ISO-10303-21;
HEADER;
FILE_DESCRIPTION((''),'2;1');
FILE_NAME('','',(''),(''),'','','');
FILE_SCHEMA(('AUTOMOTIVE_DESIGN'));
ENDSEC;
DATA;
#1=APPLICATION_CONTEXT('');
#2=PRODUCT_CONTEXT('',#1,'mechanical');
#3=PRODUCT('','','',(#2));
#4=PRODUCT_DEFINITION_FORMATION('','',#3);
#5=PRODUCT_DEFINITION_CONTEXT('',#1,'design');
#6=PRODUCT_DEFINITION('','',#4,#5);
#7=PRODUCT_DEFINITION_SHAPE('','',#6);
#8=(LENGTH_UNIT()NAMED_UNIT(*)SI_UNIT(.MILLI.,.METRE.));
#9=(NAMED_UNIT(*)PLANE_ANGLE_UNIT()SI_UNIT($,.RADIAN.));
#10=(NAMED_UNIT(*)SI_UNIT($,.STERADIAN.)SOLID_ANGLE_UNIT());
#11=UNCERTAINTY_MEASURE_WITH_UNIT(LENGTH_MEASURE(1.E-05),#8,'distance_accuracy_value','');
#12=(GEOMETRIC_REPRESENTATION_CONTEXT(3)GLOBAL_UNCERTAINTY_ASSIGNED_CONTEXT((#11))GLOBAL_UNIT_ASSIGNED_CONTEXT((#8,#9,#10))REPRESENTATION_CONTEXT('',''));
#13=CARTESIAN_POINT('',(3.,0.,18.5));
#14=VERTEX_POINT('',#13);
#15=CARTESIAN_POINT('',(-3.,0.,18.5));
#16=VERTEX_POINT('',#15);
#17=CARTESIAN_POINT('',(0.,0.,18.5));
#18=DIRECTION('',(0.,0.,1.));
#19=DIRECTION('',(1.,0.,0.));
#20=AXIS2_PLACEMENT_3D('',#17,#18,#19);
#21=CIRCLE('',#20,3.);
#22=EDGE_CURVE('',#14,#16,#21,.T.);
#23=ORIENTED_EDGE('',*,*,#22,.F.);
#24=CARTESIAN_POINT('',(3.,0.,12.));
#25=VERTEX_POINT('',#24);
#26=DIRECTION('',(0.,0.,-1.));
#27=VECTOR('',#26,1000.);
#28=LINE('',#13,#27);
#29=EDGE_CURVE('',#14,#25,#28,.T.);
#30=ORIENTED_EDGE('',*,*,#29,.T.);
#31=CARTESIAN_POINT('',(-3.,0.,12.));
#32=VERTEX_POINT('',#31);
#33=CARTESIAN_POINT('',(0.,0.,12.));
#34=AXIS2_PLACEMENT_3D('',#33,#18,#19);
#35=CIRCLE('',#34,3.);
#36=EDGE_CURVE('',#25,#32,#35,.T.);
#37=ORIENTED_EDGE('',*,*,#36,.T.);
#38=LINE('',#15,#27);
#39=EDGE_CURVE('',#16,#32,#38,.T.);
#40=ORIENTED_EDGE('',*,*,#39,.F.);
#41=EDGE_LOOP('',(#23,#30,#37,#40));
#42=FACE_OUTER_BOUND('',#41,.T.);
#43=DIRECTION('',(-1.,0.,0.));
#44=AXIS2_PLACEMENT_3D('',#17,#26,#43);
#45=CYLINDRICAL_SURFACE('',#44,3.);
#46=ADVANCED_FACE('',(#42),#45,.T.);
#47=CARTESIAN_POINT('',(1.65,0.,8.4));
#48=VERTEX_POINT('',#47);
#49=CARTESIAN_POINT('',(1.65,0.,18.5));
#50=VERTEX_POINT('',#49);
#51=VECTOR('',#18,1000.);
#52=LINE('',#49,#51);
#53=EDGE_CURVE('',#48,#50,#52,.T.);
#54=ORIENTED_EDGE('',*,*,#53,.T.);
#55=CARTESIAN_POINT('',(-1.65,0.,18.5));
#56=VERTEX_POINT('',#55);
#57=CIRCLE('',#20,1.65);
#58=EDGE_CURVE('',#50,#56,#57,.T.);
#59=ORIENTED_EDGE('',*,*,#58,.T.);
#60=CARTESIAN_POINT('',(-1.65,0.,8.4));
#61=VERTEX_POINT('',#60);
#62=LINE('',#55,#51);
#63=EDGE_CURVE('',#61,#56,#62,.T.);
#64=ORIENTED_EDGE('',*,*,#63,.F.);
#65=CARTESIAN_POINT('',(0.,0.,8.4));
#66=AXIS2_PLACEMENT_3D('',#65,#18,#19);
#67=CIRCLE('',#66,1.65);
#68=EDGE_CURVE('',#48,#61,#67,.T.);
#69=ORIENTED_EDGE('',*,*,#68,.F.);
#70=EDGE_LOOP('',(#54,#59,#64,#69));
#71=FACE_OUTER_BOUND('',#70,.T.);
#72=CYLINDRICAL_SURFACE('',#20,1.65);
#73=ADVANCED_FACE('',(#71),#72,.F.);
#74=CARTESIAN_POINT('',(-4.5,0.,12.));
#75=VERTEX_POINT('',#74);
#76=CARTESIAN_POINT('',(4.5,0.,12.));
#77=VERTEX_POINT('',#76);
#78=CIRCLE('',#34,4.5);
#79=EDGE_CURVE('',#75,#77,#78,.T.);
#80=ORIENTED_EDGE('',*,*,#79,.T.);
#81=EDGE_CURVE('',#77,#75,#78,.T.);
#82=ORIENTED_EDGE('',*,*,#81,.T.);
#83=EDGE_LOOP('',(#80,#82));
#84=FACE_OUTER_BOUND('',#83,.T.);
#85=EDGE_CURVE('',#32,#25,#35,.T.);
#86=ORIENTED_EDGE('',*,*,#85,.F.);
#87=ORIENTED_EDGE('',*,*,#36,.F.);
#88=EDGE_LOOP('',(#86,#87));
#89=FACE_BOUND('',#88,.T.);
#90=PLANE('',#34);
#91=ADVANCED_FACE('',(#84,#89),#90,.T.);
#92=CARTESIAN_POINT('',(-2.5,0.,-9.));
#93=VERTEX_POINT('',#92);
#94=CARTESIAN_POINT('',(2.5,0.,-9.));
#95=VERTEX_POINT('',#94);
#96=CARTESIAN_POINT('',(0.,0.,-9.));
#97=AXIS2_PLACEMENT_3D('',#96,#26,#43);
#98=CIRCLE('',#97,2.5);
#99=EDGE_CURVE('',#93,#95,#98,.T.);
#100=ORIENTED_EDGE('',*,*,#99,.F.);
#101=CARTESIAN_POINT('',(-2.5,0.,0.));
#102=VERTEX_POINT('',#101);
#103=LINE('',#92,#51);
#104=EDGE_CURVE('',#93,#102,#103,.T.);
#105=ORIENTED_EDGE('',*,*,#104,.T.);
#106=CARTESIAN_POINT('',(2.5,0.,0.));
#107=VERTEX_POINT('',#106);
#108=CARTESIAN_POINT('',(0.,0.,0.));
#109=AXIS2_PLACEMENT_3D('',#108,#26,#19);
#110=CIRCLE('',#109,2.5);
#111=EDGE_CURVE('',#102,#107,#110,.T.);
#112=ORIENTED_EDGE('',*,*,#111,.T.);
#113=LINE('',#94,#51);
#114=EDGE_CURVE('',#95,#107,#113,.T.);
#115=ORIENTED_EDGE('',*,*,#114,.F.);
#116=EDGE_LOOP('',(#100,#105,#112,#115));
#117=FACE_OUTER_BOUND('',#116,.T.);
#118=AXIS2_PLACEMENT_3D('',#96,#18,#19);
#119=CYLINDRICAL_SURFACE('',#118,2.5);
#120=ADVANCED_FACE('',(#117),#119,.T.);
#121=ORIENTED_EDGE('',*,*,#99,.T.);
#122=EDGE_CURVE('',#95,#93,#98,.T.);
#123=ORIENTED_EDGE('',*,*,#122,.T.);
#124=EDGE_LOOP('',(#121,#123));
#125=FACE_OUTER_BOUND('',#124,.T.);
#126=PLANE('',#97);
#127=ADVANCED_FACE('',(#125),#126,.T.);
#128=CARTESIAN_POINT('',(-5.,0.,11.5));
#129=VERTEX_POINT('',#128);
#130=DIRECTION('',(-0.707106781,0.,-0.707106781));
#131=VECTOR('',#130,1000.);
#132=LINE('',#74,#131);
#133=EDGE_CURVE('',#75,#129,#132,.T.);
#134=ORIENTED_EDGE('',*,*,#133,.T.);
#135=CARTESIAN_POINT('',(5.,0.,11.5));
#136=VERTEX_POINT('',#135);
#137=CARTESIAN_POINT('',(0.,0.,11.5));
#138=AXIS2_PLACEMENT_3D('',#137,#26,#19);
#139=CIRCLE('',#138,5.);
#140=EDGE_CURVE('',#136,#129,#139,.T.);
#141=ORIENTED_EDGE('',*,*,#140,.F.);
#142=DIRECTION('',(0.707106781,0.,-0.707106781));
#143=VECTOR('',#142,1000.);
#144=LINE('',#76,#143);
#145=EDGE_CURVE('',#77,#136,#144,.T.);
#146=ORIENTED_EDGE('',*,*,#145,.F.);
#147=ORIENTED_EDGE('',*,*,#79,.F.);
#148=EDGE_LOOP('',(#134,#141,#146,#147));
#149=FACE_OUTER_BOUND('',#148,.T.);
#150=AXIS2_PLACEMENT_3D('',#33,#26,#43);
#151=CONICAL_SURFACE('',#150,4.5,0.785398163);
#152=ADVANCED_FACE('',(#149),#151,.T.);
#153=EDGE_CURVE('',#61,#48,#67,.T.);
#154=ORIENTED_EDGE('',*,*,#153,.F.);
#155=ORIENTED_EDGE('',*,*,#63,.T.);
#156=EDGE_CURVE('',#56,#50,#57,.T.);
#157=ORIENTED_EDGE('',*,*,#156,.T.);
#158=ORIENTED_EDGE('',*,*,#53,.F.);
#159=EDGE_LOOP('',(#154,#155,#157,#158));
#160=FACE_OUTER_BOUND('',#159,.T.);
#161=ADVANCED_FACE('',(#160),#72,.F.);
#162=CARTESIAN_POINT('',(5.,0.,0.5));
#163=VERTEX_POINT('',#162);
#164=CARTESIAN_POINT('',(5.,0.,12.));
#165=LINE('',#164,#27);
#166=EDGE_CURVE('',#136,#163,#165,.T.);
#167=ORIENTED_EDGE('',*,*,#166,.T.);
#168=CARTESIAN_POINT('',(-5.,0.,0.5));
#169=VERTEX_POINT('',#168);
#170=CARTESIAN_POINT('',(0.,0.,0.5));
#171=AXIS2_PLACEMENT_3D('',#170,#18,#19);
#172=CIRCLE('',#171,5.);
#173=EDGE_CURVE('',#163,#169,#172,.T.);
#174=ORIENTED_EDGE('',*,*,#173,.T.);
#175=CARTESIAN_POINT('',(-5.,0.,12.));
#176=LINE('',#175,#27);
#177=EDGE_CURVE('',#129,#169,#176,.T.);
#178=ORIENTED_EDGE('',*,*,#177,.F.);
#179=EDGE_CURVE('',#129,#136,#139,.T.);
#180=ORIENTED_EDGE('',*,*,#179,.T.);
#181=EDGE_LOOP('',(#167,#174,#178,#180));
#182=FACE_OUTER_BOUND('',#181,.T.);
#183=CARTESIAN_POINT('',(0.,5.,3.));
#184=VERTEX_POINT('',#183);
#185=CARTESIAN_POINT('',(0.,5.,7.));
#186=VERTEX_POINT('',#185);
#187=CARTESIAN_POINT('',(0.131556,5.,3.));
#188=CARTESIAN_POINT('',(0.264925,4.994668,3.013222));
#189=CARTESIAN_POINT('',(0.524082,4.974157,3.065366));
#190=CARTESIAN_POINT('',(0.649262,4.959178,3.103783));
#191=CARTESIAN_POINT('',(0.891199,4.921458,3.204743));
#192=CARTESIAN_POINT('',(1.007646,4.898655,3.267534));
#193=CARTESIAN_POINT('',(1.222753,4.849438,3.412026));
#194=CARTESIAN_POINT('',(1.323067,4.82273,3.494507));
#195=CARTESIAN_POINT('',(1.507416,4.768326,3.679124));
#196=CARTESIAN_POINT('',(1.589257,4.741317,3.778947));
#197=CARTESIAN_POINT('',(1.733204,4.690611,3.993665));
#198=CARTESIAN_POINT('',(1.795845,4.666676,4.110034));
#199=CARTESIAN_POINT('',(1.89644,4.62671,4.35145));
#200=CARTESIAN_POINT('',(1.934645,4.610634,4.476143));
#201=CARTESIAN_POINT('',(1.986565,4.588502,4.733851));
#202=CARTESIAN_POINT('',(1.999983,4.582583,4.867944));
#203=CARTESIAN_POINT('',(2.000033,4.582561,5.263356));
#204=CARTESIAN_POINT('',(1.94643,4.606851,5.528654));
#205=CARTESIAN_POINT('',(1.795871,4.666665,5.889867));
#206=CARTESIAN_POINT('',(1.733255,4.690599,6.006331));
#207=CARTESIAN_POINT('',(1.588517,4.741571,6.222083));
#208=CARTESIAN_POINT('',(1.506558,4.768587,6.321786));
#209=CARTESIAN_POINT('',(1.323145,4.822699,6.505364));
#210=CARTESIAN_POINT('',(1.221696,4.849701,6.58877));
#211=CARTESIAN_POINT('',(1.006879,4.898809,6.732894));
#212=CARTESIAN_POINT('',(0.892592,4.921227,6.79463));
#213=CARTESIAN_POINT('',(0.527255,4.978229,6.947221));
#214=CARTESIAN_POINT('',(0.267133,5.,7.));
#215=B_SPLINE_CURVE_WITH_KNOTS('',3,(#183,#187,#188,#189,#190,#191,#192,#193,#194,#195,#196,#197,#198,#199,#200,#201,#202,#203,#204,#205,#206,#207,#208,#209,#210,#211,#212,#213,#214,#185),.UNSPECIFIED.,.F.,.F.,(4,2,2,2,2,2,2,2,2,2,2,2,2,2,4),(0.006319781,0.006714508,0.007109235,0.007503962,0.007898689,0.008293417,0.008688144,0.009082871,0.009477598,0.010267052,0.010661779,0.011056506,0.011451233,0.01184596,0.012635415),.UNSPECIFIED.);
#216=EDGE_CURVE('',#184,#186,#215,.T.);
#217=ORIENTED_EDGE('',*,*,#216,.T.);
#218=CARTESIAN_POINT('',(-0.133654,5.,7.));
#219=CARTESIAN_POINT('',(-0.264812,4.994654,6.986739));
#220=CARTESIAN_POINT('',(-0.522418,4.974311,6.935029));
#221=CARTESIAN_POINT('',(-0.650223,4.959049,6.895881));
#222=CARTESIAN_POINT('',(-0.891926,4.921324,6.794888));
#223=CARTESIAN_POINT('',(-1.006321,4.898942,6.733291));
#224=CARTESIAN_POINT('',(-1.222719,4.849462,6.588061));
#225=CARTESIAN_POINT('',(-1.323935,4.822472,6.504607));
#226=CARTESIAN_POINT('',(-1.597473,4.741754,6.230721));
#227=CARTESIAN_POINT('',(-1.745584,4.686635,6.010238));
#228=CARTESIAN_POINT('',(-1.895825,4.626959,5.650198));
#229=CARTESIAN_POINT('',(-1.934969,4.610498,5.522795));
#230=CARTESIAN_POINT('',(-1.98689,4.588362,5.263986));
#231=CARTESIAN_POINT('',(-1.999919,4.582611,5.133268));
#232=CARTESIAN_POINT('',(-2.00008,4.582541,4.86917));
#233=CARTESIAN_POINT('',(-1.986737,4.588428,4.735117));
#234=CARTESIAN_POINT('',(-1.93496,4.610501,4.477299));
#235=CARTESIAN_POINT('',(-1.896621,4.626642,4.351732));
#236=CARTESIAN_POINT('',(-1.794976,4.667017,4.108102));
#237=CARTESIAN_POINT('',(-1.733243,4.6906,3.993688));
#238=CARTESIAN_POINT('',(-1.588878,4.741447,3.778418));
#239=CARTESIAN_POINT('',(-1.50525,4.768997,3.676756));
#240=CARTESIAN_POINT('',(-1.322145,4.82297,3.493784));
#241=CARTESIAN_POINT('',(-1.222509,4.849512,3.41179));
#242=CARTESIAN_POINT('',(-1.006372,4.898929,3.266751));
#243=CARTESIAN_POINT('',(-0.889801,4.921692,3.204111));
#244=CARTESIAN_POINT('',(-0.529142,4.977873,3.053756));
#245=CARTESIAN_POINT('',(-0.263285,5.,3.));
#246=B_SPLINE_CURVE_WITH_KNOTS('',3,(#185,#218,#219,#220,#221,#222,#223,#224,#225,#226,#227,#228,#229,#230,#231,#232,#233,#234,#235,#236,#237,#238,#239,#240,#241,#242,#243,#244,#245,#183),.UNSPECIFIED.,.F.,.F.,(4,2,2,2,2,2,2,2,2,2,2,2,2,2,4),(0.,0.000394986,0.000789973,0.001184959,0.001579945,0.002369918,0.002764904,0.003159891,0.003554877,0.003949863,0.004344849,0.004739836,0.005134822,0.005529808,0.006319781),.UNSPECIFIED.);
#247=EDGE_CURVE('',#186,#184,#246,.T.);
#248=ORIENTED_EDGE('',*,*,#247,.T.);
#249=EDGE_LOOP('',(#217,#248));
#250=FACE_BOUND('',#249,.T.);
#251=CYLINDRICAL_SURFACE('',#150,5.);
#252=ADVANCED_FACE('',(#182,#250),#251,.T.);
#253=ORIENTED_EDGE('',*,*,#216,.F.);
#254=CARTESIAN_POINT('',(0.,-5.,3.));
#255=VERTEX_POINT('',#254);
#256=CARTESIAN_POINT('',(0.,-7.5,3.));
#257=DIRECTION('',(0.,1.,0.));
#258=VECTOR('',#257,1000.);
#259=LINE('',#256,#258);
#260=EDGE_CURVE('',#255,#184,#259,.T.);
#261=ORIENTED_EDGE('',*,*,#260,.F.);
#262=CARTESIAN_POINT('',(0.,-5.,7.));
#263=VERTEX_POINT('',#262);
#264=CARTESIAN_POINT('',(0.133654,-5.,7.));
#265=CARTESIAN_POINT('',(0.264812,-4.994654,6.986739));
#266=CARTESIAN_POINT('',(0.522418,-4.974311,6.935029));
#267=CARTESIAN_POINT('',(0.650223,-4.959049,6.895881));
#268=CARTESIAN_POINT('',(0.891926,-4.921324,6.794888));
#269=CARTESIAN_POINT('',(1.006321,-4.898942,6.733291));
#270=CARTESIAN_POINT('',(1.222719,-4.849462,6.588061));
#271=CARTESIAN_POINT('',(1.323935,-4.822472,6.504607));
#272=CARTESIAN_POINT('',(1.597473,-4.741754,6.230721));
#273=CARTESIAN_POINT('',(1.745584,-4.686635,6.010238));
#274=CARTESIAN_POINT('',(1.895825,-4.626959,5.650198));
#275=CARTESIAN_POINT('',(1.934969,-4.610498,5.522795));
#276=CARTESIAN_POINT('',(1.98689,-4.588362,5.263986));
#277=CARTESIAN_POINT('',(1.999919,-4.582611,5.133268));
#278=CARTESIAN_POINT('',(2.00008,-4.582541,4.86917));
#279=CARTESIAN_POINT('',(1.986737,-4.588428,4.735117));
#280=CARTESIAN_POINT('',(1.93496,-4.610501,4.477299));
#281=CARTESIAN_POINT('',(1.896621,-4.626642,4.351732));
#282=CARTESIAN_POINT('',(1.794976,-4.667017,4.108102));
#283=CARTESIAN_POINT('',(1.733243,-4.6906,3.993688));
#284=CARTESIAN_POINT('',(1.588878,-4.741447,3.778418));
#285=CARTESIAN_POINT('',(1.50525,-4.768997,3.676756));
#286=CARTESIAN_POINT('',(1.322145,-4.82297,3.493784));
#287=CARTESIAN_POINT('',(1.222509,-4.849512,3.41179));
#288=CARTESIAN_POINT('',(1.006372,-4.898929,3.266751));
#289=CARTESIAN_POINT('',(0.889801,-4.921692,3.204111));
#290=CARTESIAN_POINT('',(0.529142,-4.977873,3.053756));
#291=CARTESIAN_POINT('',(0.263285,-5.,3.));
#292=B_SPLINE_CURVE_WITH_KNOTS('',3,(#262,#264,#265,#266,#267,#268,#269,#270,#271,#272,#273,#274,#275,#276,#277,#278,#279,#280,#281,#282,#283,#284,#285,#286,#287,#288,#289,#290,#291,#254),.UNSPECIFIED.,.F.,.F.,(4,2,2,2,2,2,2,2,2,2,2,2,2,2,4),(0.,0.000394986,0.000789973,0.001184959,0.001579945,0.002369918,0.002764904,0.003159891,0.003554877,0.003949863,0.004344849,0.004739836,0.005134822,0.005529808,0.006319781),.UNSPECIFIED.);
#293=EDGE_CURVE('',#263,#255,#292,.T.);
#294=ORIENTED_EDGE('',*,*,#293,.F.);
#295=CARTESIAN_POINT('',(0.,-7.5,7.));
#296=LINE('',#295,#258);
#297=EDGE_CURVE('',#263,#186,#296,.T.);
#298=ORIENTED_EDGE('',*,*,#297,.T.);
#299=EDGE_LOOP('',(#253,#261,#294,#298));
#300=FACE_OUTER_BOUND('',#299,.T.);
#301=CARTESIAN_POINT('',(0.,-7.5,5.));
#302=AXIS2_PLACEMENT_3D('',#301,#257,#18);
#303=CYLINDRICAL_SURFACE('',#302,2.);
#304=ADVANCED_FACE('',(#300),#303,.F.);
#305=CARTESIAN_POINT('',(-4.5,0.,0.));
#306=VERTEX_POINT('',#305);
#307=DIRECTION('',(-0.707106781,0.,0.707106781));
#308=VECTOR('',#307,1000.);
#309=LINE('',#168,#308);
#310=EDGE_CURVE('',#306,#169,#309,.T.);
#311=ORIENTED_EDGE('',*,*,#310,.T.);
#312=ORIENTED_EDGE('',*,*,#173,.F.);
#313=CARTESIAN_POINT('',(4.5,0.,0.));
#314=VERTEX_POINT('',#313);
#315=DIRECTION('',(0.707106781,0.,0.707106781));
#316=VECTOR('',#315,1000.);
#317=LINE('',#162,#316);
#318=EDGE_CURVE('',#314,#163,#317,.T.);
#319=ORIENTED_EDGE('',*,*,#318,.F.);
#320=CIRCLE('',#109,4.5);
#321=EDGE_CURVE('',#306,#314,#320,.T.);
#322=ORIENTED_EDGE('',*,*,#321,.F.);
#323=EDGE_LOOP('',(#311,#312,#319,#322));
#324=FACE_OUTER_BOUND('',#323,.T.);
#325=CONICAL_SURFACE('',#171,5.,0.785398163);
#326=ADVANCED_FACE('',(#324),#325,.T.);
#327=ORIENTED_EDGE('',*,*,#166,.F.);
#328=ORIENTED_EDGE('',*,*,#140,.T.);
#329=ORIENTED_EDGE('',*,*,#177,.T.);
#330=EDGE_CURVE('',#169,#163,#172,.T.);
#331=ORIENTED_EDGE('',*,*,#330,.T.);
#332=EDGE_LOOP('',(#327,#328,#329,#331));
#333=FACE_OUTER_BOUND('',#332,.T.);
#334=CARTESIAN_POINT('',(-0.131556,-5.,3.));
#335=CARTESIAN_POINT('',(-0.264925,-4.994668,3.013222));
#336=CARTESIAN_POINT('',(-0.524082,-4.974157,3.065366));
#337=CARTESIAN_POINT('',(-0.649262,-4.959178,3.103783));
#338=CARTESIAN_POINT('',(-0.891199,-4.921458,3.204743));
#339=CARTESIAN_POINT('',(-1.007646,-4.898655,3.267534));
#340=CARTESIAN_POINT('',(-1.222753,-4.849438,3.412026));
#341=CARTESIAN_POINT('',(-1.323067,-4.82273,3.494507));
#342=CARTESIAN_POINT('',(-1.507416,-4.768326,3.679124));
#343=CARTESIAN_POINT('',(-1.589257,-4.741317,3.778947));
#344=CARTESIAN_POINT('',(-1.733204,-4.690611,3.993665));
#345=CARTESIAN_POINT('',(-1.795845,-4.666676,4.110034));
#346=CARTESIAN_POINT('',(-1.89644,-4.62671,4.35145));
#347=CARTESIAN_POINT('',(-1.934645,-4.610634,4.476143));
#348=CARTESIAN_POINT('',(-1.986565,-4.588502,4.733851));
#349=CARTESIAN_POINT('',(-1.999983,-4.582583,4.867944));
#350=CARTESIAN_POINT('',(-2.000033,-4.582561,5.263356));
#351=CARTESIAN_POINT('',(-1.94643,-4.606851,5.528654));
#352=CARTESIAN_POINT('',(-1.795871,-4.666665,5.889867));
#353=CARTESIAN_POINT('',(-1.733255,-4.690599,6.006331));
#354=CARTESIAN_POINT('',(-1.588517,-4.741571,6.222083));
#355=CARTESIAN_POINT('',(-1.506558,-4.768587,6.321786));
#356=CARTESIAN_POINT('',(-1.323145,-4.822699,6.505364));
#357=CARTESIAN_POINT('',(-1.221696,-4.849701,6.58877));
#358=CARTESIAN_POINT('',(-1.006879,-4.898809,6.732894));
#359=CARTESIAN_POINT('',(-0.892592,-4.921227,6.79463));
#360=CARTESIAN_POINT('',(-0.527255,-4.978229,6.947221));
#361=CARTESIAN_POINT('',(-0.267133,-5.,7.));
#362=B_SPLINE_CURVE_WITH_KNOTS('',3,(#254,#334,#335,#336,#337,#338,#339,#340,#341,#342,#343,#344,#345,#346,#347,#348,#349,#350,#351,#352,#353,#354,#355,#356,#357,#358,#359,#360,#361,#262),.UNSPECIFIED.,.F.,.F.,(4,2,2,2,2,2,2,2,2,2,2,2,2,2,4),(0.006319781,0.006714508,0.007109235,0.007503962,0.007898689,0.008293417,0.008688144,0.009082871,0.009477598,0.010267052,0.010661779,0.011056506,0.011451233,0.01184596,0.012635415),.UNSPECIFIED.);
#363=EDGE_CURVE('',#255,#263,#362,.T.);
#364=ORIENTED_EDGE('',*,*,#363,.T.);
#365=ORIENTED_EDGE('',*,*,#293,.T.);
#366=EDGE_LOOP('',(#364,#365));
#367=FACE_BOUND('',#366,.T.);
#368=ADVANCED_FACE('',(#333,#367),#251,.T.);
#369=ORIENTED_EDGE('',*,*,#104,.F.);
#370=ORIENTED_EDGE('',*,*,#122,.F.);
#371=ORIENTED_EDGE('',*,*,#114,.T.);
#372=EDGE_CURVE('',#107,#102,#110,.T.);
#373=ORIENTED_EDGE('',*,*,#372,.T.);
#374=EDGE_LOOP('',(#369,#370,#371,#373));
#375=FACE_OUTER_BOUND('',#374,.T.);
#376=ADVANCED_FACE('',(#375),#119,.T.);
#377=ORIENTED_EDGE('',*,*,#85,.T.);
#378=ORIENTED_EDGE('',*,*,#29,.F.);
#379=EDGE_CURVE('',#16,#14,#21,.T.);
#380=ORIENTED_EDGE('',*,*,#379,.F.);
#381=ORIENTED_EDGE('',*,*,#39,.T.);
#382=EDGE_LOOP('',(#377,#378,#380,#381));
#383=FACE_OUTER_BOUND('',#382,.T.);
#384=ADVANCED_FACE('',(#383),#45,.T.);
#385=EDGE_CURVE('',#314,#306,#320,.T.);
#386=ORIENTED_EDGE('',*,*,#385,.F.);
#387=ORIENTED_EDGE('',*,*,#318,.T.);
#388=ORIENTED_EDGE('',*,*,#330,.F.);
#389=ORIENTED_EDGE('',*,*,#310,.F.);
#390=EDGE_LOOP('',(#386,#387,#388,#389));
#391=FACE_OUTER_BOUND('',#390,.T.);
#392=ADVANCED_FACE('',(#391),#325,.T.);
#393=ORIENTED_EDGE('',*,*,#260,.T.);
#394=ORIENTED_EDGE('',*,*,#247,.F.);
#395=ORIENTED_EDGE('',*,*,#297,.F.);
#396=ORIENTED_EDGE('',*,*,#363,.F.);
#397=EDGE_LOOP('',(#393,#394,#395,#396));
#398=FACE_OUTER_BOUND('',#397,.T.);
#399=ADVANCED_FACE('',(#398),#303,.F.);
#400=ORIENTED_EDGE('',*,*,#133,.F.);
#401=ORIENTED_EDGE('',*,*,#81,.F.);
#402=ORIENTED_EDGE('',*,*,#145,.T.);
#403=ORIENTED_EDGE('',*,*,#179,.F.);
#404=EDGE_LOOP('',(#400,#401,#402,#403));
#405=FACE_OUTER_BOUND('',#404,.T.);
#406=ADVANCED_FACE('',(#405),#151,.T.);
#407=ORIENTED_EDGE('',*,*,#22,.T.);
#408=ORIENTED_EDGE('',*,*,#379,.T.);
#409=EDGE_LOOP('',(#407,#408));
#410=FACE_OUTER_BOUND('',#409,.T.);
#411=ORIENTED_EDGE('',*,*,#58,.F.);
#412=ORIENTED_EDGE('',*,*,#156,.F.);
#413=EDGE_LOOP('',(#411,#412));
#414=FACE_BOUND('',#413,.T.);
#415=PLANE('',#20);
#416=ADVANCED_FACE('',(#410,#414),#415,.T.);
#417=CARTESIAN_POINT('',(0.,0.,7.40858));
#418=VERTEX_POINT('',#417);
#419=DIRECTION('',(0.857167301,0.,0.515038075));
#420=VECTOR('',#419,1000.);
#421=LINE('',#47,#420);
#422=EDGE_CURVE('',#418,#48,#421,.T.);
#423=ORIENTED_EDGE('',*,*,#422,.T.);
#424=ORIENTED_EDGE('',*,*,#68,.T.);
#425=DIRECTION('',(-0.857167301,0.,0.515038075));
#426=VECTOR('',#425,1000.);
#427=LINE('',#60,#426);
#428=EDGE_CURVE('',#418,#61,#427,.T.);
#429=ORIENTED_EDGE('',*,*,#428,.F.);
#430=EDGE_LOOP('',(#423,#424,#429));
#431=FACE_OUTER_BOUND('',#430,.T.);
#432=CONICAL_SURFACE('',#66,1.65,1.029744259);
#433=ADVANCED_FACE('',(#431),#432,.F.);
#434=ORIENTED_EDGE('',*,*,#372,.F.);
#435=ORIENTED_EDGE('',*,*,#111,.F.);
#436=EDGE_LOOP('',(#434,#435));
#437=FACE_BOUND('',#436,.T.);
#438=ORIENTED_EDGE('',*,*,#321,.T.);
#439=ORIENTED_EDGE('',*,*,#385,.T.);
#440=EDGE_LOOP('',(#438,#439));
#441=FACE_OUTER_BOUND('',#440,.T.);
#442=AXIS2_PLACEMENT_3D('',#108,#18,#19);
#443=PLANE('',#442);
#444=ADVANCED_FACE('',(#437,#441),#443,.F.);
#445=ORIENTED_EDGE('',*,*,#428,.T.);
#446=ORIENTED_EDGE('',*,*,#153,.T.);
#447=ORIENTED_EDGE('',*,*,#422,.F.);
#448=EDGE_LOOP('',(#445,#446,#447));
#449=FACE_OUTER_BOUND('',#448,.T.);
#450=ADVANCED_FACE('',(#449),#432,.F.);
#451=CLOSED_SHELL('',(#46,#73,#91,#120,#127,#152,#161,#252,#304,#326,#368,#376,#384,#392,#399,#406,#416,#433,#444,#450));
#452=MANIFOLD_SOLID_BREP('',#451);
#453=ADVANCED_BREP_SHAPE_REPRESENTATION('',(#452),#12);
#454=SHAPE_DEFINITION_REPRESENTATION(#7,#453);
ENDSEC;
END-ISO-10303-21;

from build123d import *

# Parameters (mm, degrees)
SKETCH1_R             = 5
BOSS_EXTRUDE1_DEPTH   = 12
SKETCH2_R             = 3
BOSS_EXTRUDE2_DEPTH   = 6.5
M4_TAPPED_HOLE1_D     = 3.3
M4_TAPPED_HOLE1_DEPTH = 10.1
M4_TAPPED_HOLE1_TIP   = 0.991420021
SKETCH5_R             = 2.5
BOSS_EXTRUDE3_DEPTH   = 9
SKETCH6_R             = 2
CUT_EXTRUDE1_DEPTH    = 7.5
CHAMFER1_SIZE         = 0.5


with BuildPart() as part:
    # Sketch1 → Boss-Extrude1 (new body)
    with BuildSketch(Plane.XY):
        Circle(SKETCH1_R)
    extrude(amount=BOSS_EXTRUDE1_DEPTH)

    # Sketch2 → Boss-Extrude2 (add)
    with BuildSketch(Plane.XY.offset(12)):
        with Locations(Location((0, 0, 0), (0, 0, 180))):
            Circle(SKETCH2_R)
    extrude(amount=BOSS_EXTRUDE2_DEPTH)

    # M4 Tapped Hole1
    with Locations(Plane.XY.offset(18.5)):
        with Locations((0, 0)):
            Hole(M4_TAPPED_HOLE1_D / 2, depth=M4_TAPPED_HOLE1_DEPTH)
            with Locations((0, 0, -(M4_TAPPED_HOLE1_DEPTH + M4_TAPPED_HOLE1_TIP / 2))):  # 118° drill point
                Cone(0, M4_TAPPED_HOLE1_D / 2, M4_TAPPED_HOLE1_TIP, mode=Mode.SUBTRACT)

    # Sketch5 → Boss-Extrude3 (add)
    with BuildSketch(Plane(origin=(0, 0, 0), x_dir=(-1, 0, 0), z_dir=(0, 0, -1))):
        with Locations(Location((0, 0, 0), (0, 0, 180))):
            Circle(SKETCH5_R)
    extrude(amount=BOSS_EXTRUDE3_DEPTH)

    # Sketch6 → Cut-Extrude1 (cut, symmetric)
    with BuildSketch(Plane(origin=(0, 0, 0), x_dir=(1, 0, 0), z_dir=(0, 1, 0))):
        with Locations(Location((0, -5, 0), (0, 0, 270))):
            Circle(SKETCH6_R)
    extrude(amount=CUT_EXTRUDE1_DEPTH, both=True, mode=Mode.SUBTRACT)

    # Chamfer1
    chamfer1_edges = [part.edges().sort_by_distance(p)[0] for p in [
        (-5, 0, 0),
        (-5, 0, 12),
    ]]
    chamfer(chamfer1_edges, length=CHAMFER1_SIZE)


solid = part.part
